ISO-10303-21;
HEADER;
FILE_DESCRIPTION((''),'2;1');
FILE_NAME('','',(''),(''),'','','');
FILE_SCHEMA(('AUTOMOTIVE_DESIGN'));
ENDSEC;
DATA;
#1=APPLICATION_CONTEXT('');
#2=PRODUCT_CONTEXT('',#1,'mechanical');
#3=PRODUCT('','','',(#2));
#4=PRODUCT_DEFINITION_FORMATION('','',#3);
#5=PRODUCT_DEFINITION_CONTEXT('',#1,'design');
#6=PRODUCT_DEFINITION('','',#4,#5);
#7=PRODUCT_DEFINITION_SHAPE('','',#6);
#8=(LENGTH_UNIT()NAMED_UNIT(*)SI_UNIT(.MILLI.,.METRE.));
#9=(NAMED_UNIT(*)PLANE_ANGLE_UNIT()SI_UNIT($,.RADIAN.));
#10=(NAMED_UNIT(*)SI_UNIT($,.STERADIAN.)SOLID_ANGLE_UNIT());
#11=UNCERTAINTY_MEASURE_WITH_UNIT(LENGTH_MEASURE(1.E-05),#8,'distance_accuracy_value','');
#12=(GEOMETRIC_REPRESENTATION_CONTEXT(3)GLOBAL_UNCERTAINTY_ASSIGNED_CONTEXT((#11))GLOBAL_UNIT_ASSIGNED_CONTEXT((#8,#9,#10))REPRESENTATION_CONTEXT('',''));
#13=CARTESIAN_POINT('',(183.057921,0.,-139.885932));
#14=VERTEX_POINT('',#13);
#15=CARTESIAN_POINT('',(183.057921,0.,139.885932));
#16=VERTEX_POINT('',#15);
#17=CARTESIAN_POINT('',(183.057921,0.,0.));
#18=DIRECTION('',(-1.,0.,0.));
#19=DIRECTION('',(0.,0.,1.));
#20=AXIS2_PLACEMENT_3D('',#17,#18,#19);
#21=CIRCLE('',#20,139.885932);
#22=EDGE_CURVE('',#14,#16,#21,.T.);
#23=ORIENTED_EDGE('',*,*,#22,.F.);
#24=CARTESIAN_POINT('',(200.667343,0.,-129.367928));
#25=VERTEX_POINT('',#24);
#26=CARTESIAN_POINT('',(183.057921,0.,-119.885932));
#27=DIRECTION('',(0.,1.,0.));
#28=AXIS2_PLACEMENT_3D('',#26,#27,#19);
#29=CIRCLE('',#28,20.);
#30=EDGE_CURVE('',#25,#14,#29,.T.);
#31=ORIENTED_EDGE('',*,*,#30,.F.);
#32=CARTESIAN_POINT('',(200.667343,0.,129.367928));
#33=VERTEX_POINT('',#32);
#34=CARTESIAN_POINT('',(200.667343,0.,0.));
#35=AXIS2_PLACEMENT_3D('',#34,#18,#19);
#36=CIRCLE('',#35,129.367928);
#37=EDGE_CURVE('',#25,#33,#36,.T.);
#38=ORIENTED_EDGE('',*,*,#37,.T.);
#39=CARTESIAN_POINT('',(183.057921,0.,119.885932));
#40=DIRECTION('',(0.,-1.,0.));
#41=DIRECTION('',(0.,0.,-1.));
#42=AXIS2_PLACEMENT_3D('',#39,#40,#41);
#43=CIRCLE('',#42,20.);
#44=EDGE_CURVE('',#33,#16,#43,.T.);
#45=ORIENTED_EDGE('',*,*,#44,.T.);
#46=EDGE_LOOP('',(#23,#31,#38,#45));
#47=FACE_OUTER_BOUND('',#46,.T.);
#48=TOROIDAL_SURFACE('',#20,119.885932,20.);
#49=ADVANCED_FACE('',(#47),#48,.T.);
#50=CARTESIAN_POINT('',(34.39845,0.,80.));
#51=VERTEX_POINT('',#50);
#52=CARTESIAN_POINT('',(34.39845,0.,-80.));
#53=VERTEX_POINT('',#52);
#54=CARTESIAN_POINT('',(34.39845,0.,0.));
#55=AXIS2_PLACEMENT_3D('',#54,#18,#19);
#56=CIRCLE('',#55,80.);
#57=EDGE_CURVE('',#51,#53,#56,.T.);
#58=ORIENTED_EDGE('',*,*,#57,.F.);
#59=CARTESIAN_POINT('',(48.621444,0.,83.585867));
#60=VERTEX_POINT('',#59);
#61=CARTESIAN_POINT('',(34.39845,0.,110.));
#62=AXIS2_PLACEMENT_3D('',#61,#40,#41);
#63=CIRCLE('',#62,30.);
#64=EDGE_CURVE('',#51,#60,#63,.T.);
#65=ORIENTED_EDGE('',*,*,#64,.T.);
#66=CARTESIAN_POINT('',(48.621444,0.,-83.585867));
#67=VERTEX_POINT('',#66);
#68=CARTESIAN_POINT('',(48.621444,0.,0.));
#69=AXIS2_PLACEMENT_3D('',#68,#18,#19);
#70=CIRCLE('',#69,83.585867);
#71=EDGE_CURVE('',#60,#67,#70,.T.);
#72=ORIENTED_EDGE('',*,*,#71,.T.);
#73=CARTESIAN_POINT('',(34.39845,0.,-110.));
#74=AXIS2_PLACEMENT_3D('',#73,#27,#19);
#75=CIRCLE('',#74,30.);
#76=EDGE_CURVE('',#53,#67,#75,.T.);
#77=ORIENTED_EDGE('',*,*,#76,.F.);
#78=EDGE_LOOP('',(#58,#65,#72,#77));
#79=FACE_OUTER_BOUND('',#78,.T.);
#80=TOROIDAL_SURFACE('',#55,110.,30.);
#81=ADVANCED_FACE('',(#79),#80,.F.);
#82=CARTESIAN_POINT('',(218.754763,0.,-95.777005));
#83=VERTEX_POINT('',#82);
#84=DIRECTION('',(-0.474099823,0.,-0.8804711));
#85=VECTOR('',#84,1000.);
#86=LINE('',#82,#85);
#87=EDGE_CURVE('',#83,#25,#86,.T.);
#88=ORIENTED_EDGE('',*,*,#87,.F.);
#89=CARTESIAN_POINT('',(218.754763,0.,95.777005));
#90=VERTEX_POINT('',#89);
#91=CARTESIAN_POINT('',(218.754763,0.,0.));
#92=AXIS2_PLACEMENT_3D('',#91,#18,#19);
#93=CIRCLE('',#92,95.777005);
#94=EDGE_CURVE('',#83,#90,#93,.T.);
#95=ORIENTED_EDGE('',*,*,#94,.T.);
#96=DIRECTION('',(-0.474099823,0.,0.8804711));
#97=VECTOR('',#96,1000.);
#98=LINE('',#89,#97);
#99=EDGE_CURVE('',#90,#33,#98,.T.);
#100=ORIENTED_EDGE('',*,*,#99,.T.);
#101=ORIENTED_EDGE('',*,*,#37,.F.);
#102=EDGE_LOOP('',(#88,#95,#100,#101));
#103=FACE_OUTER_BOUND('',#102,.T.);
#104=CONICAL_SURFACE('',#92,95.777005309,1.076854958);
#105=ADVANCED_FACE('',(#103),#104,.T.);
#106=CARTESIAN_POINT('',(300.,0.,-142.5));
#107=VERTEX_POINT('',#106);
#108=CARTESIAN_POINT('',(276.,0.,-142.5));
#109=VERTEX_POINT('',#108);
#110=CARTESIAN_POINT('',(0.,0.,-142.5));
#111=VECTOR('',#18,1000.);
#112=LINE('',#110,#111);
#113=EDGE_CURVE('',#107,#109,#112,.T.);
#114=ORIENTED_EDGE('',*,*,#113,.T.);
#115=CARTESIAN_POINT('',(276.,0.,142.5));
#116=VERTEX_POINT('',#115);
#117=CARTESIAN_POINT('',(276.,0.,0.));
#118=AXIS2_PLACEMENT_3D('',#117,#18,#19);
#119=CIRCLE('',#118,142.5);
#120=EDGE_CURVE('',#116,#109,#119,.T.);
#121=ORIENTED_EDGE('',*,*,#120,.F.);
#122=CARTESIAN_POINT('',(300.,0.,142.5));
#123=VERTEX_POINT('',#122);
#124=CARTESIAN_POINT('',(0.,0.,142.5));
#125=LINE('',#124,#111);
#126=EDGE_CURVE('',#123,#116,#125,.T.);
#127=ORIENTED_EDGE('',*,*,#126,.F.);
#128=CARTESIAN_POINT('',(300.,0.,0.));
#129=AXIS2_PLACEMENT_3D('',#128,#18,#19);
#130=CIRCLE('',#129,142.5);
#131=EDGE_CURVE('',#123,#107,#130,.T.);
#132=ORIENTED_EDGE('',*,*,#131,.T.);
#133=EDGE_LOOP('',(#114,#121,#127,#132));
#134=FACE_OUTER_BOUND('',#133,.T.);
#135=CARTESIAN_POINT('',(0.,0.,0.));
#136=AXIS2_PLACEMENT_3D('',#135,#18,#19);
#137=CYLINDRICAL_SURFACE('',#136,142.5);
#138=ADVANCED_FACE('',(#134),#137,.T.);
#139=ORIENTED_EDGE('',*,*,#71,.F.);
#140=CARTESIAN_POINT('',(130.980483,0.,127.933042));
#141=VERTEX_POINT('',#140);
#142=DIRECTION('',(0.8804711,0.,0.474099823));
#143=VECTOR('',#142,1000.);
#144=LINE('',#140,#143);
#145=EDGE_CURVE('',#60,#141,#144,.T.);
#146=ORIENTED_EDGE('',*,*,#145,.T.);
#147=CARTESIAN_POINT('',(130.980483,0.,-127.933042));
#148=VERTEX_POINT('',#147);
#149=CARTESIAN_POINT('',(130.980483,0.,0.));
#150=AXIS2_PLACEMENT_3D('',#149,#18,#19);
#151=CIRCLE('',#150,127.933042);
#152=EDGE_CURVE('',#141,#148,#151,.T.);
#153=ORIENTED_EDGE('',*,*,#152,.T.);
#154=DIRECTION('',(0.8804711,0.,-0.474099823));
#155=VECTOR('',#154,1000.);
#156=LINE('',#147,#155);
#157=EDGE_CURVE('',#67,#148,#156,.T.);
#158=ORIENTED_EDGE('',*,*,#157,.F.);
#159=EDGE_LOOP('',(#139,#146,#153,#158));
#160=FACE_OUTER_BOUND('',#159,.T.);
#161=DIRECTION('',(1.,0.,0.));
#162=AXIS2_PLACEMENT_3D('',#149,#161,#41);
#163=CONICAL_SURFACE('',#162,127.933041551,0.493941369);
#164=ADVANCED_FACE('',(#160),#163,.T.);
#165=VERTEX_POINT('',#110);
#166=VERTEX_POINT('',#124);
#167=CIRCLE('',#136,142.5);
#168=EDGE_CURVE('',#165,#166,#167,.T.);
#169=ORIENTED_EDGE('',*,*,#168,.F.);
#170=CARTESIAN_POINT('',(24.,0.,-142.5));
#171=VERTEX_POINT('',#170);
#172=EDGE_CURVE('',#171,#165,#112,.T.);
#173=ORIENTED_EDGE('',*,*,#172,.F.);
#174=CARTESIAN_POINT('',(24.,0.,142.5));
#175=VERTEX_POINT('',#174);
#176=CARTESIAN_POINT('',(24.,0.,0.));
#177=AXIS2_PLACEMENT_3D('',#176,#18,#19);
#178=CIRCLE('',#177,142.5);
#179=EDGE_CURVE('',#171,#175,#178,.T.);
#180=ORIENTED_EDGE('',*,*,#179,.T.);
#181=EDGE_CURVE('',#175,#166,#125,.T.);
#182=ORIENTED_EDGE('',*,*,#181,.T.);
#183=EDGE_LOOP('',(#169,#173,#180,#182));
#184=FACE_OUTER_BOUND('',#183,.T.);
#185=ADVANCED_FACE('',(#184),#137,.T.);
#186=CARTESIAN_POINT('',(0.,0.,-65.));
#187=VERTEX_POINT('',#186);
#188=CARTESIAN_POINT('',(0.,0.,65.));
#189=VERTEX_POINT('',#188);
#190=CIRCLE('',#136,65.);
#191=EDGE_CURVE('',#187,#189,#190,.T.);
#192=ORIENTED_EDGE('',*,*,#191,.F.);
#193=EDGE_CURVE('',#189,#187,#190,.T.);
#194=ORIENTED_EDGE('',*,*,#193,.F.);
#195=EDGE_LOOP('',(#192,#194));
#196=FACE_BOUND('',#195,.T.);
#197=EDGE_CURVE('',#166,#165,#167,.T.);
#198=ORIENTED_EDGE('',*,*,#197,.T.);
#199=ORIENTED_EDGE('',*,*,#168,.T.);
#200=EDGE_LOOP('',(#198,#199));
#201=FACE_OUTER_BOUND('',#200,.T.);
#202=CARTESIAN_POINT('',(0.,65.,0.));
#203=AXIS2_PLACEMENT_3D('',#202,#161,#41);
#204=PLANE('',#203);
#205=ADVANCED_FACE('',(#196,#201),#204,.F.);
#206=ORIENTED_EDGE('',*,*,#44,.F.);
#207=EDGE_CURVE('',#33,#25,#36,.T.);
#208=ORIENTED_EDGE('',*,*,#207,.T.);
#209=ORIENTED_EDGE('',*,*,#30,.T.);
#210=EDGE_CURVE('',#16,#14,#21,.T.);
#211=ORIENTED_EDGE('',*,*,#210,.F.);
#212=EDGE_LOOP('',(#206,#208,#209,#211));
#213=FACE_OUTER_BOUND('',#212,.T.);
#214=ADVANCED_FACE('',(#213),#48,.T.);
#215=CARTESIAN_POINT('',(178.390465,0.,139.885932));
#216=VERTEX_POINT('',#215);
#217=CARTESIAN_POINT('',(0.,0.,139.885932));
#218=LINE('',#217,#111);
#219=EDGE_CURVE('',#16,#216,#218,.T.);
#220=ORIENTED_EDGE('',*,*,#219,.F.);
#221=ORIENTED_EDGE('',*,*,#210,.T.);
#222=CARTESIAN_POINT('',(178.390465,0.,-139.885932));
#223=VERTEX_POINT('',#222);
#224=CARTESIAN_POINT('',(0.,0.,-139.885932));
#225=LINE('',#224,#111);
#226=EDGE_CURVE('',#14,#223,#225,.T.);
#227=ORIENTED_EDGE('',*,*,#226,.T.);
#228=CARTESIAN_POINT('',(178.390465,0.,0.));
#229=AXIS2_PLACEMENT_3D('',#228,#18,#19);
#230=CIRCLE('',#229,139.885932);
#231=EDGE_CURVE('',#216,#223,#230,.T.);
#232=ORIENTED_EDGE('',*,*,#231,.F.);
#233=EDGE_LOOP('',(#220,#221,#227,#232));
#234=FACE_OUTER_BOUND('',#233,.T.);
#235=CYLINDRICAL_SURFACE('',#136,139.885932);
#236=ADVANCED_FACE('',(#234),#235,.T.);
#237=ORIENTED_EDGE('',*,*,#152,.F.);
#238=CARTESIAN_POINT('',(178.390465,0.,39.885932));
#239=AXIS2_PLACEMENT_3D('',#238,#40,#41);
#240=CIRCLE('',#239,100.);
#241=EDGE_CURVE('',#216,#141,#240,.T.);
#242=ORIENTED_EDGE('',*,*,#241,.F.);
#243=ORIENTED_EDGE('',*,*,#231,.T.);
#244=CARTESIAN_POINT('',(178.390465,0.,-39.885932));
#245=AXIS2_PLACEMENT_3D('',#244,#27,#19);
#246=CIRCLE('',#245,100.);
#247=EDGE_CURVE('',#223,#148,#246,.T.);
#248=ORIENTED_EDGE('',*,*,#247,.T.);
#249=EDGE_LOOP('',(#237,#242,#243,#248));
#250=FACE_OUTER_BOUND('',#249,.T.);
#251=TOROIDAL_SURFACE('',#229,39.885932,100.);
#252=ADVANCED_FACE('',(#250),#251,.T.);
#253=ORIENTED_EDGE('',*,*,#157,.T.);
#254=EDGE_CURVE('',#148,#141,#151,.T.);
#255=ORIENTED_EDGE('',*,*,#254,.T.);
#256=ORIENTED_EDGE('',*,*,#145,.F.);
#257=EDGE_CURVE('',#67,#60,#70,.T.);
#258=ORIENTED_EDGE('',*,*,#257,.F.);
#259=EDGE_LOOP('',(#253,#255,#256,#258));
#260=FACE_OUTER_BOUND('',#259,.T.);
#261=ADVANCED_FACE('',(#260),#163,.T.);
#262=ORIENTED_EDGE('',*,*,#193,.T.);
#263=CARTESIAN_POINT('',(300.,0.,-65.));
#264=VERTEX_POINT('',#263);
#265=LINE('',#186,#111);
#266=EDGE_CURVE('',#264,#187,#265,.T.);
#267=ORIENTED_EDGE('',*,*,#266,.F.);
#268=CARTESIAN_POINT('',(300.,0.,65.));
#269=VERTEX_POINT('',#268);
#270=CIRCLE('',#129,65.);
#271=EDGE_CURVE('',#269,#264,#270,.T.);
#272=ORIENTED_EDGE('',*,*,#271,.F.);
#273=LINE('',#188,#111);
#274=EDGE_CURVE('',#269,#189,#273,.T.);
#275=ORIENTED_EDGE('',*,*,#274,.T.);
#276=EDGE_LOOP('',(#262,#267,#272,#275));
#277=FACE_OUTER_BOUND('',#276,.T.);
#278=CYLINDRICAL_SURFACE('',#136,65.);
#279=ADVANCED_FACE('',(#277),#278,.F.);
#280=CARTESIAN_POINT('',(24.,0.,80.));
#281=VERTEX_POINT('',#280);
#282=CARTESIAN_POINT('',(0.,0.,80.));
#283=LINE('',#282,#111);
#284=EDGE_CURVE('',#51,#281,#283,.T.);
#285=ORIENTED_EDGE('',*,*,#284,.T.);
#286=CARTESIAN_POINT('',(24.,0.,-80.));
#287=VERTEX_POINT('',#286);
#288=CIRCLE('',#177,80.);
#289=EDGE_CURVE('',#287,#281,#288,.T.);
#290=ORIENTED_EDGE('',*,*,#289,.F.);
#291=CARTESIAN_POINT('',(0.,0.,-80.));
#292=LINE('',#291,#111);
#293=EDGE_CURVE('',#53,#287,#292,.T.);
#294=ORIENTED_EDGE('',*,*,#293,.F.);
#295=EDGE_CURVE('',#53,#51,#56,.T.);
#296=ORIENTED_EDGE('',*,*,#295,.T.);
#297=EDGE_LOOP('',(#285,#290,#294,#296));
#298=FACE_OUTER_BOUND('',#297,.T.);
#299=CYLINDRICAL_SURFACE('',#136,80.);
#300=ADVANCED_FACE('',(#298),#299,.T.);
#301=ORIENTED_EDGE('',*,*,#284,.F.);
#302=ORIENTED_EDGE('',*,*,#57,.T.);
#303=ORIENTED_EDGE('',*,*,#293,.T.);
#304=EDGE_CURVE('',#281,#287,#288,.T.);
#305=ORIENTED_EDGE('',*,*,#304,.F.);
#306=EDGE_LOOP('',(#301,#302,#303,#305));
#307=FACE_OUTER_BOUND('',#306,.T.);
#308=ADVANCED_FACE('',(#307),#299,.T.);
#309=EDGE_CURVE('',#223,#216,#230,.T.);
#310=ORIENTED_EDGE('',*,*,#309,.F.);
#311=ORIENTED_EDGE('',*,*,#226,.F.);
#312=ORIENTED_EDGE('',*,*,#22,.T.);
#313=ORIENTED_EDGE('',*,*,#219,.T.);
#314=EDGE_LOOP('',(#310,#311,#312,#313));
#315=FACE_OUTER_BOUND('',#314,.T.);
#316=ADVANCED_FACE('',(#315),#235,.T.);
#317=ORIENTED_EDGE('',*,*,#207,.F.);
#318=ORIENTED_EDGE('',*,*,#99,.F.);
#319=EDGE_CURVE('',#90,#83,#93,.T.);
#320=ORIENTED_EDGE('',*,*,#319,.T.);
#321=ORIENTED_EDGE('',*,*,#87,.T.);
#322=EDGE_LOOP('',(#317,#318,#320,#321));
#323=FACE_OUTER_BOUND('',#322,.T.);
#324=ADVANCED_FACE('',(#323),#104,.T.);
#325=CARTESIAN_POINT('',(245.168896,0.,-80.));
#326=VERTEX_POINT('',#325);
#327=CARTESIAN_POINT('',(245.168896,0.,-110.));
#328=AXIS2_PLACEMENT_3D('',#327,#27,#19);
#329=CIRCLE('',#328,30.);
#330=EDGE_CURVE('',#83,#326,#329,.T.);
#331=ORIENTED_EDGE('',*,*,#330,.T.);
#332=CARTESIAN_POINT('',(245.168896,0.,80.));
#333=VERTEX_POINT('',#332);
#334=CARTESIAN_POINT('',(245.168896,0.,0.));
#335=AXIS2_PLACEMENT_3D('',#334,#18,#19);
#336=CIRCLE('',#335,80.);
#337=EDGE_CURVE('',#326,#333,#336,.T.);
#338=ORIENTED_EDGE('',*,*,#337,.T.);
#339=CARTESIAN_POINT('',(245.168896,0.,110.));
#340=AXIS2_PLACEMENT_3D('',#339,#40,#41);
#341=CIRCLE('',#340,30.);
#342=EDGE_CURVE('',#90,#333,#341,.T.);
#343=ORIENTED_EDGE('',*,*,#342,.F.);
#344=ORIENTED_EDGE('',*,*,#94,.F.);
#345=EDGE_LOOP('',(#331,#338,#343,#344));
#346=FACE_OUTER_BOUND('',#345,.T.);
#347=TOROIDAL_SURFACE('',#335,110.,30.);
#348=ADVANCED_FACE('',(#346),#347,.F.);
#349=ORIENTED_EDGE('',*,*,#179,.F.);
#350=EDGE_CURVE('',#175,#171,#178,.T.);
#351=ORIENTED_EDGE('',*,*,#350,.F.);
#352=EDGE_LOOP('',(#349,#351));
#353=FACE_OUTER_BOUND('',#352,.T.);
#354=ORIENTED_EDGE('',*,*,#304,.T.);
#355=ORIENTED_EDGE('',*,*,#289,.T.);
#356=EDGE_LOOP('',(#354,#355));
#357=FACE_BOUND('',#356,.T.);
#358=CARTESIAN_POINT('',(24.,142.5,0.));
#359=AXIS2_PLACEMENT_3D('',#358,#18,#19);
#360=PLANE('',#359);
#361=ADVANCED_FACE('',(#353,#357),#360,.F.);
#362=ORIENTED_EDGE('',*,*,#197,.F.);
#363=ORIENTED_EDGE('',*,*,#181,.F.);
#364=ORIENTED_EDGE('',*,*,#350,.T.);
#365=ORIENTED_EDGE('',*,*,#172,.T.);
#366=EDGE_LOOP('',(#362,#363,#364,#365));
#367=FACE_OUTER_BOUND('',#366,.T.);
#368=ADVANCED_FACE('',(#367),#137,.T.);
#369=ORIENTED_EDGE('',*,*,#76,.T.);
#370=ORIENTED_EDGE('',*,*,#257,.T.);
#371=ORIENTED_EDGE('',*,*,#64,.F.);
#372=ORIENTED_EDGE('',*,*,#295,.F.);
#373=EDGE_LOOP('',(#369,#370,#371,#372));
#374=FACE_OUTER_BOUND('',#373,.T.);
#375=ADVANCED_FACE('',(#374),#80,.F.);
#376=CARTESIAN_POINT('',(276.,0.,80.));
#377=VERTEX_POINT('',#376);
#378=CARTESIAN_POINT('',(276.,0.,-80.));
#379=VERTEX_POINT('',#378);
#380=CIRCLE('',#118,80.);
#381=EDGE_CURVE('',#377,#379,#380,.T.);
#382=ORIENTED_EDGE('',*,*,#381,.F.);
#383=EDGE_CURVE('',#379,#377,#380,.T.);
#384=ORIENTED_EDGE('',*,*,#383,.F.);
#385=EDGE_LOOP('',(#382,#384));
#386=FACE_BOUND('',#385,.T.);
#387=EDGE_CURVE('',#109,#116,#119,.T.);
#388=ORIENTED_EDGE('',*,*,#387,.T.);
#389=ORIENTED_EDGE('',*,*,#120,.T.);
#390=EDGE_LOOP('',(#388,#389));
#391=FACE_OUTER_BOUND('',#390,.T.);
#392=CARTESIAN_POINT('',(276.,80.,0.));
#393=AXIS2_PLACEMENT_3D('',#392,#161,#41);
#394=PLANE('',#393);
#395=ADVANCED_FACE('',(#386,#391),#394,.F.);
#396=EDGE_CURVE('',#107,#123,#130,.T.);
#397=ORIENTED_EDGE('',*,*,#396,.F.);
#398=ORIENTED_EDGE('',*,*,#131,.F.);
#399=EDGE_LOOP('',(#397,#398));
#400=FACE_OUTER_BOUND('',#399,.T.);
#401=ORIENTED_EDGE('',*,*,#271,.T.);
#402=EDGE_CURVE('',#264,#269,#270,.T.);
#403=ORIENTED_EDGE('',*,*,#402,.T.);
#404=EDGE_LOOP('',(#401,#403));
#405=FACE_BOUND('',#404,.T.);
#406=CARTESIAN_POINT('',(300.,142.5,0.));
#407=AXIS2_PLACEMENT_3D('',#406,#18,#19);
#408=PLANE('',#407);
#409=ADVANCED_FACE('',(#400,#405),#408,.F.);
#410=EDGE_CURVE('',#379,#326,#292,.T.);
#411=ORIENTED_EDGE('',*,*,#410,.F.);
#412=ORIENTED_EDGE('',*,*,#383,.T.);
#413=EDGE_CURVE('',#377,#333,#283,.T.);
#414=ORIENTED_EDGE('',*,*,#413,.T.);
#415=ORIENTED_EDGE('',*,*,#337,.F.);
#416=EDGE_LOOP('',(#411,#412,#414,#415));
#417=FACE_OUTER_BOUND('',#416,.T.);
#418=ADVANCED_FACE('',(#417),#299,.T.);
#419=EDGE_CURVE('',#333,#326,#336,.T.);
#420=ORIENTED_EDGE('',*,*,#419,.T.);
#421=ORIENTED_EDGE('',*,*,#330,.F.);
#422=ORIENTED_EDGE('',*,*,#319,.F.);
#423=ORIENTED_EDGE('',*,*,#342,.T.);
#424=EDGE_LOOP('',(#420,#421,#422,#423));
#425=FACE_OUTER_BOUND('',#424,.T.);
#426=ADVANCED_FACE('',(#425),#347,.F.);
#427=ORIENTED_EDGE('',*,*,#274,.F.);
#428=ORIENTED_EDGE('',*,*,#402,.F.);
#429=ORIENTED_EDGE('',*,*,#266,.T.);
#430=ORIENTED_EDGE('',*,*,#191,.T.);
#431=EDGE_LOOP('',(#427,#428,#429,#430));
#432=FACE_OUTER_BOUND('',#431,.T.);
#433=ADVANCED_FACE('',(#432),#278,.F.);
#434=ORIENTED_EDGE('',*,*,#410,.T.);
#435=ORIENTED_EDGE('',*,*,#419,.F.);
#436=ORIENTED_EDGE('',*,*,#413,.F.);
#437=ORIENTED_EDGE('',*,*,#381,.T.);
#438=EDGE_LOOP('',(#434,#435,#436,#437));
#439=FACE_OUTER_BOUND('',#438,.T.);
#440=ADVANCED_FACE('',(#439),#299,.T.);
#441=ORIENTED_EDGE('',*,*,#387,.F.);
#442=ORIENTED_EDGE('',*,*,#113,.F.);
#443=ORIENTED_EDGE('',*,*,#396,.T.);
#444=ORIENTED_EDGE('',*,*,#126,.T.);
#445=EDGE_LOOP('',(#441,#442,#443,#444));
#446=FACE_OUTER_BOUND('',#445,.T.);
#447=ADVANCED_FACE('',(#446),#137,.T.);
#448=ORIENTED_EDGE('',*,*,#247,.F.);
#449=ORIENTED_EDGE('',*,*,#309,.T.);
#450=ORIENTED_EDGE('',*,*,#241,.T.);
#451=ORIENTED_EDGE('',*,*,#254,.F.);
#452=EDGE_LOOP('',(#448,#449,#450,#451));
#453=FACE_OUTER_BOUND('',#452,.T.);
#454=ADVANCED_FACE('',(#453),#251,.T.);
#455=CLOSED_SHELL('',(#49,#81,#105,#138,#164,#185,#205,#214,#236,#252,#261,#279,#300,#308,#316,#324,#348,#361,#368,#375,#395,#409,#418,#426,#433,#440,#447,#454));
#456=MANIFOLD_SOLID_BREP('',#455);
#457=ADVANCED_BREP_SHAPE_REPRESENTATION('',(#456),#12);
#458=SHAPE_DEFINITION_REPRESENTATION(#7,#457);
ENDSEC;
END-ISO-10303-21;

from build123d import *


with BuildPart() as part:
    # Sketch1 → Revolve1 (revolve)
    with BuildSketch(Plane.XY, mode=Mode.PRIVATE) as revolve1_sk:
        with BuildLine():
            Line((0, 65), (0, 142.5))
            Line((0, 142.5), (24, 142.5))
            Line((24, 142.5), (24, 80))
            Line((24, 80), (34.398449785, 80))
            ThreePointArc((34.398449785, 80), (41.732480398, 80.910276815), (48.621444476, 83.585867002))
            Line((48.621444476, 83.585867002), (130.980482924, 127.933041551))
            ThreePointArc((130.980482924, 127.933041551), (153.943696517, 136.851675508), (178.390465228, 139.885931559))
            Line((178.390465228, 139.885931559), (183.05792065, 139.885931559))
            ThreePointArc((183.05792065, 139.885931559), (193.313652481, 137.056253763), (200.667342649, 129.36792802))
            Line((200.667342649, 129.36792802), (218.75476257, 95.777005309))
            ThreePointArc((218.75476257, 95.777005309), (229.785297821, 84.244516693), (245.168895567, 80))
            Line((245.168895567, 80), (276, 80))
            Line((276, 80), (276, 142.5))
            Line((276, 142.5), (300, 142.5))
            Line((300, 142.5), (300, 65))
            Line((300, 65), (0, 65))
        make_face()
    revolve(revolve1_sk.sketch.rotate(Axis((0, 0, 0), (1, 0, 0)), 90), axis=Axis((0, 0, 0), (1, 0, 0)))


solid = part.part
